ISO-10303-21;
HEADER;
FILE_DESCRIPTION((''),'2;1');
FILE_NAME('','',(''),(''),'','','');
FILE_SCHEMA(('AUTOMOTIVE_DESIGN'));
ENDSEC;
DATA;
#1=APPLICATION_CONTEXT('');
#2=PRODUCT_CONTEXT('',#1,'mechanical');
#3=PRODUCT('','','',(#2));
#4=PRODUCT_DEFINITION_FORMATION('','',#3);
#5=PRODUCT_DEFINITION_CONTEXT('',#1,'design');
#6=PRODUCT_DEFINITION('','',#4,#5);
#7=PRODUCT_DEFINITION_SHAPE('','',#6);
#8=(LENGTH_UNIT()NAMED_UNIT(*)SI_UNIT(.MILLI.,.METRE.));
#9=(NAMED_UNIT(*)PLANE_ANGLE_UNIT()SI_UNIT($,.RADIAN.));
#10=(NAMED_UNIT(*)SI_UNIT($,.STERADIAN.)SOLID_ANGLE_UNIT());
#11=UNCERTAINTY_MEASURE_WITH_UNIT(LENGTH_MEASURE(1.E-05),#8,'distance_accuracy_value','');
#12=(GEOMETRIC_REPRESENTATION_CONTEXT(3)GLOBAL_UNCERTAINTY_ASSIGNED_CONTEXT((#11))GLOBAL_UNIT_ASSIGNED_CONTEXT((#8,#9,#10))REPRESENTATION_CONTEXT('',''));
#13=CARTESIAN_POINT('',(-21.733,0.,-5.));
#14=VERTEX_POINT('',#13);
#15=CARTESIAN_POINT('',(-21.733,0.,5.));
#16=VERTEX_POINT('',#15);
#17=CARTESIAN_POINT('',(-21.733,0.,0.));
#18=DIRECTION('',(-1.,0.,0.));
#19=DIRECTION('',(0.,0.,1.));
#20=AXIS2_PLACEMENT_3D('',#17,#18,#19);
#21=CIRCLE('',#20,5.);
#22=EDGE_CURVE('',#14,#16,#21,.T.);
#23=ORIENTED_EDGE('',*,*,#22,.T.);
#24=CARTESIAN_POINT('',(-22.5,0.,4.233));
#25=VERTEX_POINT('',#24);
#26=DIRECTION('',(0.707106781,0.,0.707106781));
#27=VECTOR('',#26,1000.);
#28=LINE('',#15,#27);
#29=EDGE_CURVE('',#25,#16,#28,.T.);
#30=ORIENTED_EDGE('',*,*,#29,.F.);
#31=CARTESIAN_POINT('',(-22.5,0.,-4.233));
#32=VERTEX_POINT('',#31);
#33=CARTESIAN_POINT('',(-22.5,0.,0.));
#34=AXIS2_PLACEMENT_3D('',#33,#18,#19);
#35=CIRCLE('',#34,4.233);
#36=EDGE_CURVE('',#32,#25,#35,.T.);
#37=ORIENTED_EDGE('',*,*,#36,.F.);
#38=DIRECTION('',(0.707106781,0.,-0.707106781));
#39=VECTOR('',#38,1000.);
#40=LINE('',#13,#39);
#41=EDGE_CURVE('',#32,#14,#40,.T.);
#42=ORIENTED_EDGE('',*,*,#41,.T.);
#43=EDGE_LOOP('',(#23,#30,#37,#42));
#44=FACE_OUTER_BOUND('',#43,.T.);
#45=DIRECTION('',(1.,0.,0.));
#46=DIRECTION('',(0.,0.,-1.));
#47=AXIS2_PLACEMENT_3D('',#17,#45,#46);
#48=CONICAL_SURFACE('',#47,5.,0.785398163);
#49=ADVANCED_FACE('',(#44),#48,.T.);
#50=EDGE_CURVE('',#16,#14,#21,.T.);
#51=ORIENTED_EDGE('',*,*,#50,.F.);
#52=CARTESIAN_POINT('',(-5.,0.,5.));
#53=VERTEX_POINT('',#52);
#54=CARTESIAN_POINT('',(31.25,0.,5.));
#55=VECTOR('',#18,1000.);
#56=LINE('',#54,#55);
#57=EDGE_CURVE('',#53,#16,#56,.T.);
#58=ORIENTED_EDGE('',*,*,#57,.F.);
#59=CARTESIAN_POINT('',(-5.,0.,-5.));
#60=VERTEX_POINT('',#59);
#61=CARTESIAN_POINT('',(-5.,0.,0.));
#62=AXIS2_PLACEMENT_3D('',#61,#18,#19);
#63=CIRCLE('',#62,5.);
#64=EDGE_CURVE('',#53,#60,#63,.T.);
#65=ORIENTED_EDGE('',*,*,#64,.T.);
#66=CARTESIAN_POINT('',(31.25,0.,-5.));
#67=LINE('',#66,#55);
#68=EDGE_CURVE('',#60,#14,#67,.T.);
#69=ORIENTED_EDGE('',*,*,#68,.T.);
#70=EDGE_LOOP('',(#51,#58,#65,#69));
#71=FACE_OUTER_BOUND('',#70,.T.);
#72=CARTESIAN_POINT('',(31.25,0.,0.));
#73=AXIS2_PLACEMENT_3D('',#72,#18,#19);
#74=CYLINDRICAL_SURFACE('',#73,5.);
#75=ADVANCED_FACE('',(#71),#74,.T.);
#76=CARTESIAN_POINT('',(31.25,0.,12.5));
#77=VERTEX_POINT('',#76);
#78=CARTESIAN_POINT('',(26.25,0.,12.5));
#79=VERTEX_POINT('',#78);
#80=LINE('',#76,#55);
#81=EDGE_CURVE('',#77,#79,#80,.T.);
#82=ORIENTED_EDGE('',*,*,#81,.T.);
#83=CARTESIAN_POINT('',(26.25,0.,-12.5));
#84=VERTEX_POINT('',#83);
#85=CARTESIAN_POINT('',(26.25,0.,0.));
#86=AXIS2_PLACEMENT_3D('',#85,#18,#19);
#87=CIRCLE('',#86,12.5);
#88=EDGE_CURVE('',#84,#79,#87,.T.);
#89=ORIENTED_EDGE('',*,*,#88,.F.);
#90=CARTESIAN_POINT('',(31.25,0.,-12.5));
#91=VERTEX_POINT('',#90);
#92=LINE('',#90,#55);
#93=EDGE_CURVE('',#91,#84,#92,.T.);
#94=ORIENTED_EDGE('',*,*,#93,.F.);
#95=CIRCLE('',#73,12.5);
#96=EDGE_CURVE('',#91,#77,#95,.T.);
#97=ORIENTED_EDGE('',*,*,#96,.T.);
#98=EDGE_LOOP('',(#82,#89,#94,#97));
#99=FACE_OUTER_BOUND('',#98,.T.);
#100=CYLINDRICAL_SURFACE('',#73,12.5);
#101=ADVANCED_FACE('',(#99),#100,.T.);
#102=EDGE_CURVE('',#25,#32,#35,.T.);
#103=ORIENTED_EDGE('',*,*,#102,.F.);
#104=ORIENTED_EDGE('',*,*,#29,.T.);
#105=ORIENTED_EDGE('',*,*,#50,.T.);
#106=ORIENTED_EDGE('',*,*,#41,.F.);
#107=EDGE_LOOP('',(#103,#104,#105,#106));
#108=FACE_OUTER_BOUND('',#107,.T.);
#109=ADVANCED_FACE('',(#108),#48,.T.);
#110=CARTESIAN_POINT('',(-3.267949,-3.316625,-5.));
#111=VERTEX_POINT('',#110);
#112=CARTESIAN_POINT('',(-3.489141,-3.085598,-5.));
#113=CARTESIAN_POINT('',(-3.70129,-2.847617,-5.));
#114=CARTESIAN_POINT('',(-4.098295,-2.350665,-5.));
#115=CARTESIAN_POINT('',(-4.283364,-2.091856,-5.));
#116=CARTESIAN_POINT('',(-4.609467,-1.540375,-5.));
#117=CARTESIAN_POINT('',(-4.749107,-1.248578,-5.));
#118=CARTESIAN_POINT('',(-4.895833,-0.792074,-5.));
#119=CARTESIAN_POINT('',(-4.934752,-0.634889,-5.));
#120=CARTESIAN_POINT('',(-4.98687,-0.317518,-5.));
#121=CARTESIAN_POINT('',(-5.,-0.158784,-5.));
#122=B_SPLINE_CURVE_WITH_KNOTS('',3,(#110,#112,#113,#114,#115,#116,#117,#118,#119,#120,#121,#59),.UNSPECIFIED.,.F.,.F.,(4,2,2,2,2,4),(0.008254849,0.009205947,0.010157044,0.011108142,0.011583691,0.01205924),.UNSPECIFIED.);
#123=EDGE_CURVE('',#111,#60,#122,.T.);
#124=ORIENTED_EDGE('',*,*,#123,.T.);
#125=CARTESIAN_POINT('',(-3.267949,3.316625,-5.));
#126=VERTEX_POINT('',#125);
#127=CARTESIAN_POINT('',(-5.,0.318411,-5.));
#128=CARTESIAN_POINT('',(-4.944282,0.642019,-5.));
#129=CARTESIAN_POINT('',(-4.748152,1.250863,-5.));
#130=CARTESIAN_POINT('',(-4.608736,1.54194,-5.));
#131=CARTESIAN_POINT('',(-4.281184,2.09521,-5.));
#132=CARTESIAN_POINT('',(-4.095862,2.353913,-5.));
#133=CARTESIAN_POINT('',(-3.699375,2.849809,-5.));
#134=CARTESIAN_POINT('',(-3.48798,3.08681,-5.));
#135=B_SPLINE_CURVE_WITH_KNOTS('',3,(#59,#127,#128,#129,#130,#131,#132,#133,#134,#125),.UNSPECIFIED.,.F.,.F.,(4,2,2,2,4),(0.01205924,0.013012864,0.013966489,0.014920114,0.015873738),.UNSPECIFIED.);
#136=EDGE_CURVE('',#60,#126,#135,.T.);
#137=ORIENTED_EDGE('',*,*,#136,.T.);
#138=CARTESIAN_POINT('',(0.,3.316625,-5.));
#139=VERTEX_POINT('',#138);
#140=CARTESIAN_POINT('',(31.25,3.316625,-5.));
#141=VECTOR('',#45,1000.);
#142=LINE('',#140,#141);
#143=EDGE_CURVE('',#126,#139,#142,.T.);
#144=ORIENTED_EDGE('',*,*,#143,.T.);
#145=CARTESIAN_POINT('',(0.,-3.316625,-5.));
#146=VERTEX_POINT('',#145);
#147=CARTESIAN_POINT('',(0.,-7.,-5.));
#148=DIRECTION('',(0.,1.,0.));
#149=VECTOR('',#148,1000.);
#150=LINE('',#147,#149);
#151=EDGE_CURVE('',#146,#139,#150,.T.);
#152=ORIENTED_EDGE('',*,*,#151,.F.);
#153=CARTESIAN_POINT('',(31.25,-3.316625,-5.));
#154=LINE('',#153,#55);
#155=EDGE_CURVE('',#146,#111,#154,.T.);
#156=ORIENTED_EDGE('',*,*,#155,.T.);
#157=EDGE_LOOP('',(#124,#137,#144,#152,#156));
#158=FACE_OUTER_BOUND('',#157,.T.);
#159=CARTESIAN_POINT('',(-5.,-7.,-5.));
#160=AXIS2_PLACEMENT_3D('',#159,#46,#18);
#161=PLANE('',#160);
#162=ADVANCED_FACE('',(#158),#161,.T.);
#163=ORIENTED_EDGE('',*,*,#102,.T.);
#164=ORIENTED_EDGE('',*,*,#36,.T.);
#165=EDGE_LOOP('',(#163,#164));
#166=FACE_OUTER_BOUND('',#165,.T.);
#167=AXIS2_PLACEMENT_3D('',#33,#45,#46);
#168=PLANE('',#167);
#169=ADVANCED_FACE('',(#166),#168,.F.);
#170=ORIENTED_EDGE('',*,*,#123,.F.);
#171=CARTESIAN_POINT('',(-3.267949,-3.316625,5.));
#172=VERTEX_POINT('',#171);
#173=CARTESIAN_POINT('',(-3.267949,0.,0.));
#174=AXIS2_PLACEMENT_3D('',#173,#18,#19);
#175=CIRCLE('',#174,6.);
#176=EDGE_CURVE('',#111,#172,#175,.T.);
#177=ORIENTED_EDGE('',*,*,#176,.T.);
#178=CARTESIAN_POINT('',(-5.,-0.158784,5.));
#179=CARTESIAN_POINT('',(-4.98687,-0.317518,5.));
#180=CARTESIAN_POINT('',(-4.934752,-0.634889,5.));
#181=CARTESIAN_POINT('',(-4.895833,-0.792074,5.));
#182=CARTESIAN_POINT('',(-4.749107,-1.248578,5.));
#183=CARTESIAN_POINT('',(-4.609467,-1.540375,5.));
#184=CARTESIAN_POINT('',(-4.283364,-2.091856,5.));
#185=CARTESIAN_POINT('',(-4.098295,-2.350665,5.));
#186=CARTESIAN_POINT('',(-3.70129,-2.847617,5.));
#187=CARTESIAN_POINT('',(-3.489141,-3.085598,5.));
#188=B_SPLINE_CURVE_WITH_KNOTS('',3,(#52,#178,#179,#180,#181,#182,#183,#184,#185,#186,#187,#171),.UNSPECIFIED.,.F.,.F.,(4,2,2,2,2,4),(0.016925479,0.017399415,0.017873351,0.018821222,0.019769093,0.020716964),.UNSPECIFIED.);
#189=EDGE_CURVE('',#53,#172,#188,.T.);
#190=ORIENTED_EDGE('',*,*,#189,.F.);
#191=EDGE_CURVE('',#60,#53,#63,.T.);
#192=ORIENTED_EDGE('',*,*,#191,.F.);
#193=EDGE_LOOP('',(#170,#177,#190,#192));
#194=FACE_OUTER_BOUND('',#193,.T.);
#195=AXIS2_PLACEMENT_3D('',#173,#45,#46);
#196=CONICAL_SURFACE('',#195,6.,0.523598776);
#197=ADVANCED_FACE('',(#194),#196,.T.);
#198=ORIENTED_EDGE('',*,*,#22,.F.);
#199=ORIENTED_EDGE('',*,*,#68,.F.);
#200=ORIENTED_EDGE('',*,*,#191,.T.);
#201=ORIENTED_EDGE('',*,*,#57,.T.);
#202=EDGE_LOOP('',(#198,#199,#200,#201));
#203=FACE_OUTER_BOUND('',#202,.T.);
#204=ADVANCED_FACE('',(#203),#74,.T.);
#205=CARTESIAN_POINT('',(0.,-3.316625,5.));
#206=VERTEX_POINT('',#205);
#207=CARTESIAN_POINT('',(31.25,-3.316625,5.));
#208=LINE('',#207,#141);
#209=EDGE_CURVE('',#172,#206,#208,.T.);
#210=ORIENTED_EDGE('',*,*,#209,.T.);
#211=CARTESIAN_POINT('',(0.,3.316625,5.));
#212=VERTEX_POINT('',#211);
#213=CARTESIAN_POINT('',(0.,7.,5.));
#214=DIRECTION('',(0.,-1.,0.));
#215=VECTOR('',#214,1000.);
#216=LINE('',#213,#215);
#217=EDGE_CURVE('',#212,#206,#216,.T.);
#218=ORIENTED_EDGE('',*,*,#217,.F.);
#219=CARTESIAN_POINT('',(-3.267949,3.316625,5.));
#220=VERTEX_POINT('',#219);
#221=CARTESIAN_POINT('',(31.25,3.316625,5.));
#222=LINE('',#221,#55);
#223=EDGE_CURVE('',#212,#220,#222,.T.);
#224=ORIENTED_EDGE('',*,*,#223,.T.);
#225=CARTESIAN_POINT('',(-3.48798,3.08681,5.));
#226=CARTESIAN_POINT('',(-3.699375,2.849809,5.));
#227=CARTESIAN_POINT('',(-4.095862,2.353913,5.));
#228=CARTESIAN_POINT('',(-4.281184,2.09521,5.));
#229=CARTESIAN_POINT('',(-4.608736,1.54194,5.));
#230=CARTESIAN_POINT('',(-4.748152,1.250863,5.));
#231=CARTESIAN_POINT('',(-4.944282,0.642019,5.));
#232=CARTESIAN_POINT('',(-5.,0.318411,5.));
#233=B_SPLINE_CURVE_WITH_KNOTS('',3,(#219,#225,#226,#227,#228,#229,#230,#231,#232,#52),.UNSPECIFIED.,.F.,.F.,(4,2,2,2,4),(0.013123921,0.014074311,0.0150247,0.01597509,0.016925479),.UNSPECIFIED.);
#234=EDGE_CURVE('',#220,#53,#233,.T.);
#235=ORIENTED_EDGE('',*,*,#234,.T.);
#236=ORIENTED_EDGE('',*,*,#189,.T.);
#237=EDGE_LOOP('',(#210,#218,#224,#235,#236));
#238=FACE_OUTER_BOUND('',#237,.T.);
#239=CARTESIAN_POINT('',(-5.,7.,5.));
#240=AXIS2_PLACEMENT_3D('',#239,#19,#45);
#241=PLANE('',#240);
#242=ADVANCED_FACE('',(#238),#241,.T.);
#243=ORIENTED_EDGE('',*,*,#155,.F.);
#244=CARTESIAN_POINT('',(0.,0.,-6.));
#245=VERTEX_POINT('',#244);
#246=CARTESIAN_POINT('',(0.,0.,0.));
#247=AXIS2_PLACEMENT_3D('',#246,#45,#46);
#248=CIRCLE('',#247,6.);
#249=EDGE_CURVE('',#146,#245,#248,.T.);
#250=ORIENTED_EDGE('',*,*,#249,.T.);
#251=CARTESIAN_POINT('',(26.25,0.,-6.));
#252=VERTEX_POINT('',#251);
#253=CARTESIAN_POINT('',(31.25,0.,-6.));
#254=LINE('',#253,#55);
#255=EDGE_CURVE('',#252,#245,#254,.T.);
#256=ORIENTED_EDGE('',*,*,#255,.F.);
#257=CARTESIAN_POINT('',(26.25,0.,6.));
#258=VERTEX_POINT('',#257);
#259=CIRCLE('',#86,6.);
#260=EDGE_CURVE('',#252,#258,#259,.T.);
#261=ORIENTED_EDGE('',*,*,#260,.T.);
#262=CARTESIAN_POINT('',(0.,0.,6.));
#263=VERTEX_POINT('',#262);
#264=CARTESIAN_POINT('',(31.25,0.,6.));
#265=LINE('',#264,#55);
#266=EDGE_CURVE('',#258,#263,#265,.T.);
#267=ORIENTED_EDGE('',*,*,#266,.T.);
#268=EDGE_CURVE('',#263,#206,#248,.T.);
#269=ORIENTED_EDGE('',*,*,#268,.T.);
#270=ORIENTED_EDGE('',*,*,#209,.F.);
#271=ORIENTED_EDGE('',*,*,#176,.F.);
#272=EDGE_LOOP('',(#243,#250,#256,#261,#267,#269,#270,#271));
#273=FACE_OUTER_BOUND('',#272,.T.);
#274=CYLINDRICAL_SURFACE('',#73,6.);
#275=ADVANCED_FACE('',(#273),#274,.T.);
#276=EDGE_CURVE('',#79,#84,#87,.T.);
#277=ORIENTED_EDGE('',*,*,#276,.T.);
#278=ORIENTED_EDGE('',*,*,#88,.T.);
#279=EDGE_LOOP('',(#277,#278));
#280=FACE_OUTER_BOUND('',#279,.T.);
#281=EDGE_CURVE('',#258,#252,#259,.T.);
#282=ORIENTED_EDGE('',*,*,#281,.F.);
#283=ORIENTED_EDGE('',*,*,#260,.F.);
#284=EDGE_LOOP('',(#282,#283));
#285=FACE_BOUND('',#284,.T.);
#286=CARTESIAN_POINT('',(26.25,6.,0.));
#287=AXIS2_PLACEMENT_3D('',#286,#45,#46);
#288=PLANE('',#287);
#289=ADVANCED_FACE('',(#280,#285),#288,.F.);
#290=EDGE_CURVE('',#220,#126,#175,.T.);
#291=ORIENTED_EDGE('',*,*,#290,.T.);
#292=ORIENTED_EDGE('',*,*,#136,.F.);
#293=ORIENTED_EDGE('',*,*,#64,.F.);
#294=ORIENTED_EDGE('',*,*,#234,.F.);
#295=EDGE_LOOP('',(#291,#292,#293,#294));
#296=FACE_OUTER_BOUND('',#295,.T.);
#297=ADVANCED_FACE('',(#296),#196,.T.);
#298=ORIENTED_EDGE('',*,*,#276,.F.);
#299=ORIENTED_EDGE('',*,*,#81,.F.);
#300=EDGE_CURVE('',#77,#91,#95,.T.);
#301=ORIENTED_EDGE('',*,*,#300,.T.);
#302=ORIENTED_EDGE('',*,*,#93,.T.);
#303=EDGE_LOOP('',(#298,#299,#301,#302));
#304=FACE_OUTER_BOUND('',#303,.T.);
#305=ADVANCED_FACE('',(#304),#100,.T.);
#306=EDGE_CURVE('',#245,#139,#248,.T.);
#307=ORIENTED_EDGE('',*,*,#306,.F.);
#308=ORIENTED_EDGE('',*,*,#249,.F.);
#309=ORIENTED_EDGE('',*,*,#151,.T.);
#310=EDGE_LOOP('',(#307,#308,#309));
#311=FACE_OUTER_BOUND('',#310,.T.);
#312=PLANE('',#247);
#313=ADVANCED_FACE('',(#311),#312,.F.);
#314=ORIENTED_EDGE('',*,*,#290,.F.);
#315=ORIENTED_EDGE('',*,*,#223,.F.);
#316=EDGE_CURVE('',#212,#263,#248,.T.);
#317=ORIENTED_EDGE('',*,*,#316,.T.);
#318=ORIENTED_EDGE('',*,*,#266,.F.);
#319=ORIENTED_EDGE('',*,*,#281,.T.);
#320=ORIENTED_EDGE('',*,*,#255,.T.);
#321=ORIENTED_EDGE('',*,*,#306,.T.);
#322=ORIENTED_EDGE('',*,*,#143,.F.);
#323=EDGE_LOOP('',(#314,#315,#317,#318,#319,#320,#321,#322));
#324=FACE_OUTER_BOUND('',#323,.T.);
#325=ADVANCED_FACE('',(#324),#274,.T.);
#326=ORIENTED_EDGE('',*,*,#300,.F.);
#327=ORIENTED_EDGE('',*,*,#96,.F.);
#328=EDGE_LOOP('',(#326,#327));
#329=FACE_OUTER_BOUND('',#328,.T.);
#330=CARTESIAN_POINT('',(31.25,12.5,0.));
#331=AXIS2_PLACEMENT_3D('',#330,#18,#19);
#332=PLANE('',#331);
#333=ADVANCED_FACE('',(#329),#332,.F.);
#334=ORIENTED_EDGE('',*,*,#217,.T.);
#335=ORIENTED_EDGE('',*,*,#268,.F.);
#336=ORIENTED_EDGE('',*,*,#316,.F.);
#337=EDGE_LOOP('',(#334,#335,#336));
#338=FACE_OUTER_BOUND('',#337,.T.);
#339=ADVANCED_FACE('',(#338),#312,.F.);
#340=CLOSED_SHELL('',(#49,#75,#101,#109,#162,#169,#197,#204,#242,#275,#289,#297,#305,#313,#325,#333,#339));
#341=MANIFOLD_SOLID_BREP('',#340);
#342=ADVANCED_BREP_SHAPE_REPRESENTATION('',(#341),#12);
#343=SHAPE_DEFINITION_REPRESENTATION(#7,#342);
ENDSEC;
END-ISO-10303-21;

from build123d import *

# Parameters (mm, degrees)
SKETCH2_R          = 12
SKETCH2_W          = 10
SKETCH2_H          = 14
CUT_EXTRUDE1_DEPTH = 5


with BuildPart() as part:
    # Sketch1 → Revolve1 (revolve)
    with BuildSketch(Plane.XY, mode=Mode.PRIVATE) as revolve1_sk:
        Polygon((-22.5, 0), (-22.5, 4.233), (-21.733, 5), (-5, 5), (-3.267949192, 6), (26.25, 6), (26.25, 12.5), (31.25, 12.5), (31.25, 0), align=None)
    revolve(revolve1_sk.sketch.rotate(Axis((31.25, 0, 0), (-1, 0, 0)), 270), axis=Axis((31.25, 0, 0), (-1, 0, 0)))

    # Sketch2 → Cut-Extrude1 (cut)
    with BuildSketch(Plane(origin=(0, 0, 0), x_dir=(0, 0, -1), z_dir=(1, 0, 0))):
        Circle(SKETCH2_R)
        Rectangle(SKETCH2_W, SKETCH2_H, mode=Mode.SUBTRACT)
    extrude(amount=-CUT_EXTRUDE1_DEPTH, mode=Mode.SUBTRACT)


solid = part.part
